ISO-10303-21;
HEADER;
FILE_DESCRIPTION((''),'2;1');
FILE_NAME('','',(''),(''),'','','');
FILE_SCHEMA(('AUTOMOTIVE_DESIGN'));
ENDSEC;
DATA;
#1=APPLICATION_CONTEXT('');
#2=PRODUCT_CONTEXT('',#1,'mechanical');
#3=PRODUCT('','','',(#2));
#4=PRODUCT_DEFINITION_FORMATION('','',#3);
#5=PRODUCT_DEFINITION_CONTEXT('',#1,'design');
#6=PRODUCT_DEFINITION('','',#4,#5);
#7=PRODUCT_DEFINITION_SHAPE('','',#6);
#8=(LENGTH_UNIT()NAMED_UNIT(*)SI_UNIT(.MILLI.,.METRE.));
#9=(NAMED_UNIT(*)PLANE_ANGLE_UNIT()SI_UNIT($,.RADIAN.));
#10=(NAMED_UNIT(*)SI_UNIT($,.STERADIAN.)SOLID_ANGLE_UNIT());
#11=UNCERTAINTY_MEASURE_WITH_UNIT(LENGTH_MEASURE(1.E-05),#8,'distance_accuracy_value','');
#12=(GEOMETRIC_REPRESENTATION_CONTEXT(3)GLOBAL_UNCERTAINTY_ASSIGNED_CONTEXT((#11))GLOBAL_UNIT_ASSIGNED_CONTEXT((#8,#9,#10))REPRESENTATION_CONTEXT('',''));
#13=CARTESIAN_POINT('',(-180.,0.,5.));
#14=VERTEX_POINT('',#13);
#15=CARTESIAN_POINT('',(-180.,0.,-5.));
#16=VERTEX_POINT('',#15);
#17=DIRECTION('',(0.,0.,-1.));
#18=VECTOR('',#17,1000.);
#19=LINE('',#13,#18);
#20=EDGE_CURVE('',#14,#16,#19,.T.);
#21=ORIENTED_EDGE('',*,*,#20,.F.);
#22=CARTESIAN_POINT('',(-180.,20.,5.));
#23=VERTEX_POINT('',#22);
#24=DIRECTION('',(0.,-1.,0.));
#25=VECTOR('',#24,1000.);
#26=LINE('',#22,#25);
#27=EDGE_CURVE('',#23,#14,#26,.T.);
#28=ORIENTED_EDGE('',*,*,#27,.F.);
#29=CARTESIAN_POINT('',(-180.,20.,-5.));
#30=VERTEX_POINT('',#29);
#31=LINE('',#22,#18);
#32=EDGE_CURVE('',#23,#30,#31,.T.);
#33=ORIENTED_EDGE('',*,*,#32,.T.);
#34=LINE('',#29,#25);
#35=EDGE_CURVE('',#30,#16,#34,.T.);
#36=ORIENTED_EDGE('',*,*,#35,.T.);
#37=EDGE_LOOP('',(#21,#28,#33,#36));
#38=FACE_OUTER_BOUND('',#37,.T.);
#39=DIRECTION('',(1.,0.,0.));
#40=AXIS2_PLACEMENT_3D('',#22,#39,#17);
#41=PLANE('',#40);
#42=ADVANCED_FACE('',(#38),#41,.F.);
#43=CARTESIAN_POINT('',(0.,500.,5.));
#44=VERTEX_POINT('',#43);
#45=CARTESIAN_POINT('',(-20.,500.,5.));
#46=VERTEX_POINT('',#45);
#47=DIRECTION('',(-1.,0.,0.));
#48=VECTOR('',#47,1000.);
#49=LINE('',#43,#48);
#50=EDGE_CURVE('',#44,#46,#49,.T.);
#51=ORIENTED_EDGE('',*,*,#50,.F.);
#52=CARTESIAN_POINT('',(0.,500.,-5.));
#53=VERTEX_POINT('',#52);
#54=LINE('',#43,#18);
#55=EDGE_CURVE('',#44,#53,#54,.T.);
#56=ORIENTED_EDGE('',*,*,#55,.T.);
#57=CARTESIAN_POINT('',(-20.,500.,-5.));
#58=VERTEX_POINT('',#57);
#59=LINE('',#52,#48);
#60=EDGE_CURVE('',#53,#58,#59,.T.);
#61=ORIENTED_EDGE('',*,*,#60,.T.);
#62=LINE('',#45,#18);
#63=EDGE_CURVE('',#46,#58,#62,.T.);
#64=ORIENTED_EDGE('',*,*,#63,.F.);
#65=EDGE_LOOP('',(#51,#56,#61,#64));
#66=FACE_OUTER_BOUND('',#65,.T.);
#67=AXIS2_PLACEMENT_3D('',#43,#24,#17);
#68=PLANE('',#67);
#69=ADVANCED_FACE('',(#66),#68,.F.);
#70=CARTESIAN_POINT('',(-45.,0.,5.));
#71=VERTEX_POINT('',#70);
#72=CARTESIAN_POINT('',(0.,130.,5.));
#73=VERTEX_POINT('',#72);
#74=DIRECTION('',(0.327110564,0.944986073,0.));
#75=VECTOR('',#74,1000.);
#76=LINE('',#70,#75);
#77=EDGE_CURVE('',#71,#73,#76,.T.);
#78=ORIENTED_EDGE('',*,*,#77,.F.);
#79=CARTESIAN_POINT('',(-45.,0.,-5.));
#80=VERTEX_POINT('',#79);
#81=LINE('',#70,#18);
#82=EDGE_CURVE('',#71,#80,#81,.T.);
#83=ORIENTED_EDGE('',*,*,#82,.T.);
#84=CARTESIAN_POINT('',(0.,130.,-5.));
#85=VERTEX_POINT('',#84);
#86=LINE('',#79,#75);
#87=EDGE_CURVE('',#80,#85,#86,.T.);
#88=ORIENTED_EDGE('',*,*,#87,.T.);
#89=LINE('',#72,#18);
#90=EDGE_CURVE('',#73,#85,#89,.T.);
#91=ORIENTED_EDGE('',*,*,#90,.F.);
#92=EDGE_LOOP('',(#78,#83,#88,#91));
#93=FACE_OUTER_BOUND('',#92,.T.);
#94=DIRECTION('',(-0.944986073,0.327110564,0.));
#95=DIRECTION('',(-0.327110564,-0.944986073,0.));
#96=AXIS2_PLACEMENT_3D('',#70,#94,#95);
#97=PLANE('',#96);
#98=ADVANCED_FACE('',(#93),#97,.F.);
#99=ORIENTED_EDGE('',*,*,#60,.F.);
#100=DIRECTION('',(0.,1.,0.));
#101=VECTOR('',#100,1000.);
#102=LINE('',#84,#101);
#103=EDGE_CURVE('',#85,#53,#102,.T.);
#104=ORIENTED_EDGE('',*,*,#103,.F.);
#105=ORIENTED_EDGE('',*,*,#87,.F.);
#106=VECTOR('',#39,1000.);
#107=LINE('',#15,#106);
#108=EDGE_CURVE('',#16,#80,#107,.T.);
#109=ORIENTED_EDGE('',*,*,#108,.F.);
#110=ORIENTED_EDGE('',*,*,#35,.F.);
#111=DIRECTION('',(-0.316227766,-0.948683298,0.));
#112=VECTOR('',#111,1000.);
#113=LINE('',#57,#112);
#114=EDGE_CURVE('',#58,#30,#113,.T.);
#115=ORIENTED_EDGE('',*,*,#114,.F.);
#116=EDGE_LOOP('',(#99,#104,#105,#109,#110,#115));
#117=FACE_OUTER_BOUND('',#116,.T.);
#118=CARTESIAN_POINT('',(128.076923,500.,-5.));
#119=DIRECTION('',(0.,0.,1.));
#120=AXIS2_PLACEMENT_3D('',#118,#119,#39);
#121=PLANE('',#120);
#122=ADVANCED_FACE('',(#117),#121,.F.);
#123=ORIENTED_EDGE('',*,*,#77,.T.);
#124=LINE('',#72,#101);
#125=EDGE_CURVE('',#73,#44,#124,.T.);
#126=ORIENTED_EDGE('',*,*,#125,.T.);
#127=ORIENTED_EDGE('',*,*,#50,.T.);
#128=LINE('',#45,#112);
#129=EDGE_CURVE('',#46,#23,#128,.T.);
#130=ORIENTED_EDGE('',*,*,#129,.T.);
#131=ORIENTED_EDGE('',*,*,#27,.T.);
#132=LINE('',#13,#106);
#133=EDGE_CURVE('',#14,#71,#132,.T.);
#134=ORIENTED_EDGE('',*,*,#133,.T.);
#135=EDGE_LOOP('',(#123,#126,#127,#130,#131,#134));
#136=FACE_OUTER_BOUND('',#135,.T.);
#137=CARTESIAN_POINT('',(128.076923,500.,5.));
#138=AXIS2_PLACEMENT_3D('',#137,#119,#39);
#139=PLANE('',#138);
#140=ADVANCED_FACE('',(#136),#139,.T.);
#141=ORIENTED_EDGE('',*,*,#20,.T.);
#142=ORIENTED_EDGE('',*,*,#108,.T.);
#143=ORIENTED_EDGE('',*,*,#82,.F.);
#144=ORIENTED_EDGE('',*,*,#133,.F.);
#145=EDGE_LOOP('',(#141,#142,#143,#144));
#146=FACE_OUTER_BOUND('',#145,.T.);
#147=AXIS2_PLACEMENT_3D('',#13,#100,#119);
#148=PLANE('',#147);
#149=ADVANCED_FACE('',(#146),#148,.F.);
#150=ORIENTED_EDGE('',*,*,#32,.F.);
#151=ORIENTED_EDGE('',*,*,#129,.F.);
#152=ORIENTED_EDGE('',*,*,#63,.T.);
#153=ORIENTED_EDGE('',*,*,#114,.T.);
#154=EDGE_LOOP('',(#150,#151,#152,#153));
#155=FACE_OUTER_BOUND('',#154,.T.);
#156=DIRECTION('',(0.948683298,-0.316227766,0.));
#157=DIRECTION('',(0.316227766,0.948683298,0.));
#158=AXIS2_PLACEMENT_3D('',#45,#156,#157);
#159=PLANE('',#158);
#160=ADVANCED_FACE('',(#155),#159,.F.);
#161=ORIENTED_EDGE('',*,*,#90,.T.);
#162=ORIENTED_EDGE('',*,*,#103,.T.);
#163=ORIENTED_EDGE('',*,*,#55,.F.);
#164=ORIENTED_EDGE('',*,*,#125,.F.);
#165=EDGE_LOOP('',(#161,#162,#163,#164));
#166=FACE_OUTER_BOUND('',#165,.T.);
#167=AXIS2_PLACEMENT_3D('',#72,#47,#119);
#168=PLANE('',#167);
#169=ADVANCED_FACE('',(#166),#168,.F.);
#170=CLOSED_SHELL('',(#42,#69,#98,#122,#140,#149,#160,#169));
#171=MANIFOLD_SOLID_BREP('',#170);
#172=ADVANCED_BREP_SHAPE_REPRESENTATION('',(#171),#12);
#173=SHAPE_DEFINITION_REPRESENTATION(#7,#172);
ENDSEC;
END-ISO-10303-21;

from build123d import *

# Parameters (mm, degrees)
BOSS_EXTRUDE1_DEPTH = 5


with BuildPart() as part:
    # Sketch1 → Boss-Extrude1 (new, symmetric)
    with BuildSketch(Plane.XY):
        Polygon((0, 130), (0, 500), (-20, 500), (-180, 20), (-180, 0), (-45, 0), align=None)
    extrude(amount=BOSS_EXTRUDE1_DEPTH, both=True)


solid = part.part
